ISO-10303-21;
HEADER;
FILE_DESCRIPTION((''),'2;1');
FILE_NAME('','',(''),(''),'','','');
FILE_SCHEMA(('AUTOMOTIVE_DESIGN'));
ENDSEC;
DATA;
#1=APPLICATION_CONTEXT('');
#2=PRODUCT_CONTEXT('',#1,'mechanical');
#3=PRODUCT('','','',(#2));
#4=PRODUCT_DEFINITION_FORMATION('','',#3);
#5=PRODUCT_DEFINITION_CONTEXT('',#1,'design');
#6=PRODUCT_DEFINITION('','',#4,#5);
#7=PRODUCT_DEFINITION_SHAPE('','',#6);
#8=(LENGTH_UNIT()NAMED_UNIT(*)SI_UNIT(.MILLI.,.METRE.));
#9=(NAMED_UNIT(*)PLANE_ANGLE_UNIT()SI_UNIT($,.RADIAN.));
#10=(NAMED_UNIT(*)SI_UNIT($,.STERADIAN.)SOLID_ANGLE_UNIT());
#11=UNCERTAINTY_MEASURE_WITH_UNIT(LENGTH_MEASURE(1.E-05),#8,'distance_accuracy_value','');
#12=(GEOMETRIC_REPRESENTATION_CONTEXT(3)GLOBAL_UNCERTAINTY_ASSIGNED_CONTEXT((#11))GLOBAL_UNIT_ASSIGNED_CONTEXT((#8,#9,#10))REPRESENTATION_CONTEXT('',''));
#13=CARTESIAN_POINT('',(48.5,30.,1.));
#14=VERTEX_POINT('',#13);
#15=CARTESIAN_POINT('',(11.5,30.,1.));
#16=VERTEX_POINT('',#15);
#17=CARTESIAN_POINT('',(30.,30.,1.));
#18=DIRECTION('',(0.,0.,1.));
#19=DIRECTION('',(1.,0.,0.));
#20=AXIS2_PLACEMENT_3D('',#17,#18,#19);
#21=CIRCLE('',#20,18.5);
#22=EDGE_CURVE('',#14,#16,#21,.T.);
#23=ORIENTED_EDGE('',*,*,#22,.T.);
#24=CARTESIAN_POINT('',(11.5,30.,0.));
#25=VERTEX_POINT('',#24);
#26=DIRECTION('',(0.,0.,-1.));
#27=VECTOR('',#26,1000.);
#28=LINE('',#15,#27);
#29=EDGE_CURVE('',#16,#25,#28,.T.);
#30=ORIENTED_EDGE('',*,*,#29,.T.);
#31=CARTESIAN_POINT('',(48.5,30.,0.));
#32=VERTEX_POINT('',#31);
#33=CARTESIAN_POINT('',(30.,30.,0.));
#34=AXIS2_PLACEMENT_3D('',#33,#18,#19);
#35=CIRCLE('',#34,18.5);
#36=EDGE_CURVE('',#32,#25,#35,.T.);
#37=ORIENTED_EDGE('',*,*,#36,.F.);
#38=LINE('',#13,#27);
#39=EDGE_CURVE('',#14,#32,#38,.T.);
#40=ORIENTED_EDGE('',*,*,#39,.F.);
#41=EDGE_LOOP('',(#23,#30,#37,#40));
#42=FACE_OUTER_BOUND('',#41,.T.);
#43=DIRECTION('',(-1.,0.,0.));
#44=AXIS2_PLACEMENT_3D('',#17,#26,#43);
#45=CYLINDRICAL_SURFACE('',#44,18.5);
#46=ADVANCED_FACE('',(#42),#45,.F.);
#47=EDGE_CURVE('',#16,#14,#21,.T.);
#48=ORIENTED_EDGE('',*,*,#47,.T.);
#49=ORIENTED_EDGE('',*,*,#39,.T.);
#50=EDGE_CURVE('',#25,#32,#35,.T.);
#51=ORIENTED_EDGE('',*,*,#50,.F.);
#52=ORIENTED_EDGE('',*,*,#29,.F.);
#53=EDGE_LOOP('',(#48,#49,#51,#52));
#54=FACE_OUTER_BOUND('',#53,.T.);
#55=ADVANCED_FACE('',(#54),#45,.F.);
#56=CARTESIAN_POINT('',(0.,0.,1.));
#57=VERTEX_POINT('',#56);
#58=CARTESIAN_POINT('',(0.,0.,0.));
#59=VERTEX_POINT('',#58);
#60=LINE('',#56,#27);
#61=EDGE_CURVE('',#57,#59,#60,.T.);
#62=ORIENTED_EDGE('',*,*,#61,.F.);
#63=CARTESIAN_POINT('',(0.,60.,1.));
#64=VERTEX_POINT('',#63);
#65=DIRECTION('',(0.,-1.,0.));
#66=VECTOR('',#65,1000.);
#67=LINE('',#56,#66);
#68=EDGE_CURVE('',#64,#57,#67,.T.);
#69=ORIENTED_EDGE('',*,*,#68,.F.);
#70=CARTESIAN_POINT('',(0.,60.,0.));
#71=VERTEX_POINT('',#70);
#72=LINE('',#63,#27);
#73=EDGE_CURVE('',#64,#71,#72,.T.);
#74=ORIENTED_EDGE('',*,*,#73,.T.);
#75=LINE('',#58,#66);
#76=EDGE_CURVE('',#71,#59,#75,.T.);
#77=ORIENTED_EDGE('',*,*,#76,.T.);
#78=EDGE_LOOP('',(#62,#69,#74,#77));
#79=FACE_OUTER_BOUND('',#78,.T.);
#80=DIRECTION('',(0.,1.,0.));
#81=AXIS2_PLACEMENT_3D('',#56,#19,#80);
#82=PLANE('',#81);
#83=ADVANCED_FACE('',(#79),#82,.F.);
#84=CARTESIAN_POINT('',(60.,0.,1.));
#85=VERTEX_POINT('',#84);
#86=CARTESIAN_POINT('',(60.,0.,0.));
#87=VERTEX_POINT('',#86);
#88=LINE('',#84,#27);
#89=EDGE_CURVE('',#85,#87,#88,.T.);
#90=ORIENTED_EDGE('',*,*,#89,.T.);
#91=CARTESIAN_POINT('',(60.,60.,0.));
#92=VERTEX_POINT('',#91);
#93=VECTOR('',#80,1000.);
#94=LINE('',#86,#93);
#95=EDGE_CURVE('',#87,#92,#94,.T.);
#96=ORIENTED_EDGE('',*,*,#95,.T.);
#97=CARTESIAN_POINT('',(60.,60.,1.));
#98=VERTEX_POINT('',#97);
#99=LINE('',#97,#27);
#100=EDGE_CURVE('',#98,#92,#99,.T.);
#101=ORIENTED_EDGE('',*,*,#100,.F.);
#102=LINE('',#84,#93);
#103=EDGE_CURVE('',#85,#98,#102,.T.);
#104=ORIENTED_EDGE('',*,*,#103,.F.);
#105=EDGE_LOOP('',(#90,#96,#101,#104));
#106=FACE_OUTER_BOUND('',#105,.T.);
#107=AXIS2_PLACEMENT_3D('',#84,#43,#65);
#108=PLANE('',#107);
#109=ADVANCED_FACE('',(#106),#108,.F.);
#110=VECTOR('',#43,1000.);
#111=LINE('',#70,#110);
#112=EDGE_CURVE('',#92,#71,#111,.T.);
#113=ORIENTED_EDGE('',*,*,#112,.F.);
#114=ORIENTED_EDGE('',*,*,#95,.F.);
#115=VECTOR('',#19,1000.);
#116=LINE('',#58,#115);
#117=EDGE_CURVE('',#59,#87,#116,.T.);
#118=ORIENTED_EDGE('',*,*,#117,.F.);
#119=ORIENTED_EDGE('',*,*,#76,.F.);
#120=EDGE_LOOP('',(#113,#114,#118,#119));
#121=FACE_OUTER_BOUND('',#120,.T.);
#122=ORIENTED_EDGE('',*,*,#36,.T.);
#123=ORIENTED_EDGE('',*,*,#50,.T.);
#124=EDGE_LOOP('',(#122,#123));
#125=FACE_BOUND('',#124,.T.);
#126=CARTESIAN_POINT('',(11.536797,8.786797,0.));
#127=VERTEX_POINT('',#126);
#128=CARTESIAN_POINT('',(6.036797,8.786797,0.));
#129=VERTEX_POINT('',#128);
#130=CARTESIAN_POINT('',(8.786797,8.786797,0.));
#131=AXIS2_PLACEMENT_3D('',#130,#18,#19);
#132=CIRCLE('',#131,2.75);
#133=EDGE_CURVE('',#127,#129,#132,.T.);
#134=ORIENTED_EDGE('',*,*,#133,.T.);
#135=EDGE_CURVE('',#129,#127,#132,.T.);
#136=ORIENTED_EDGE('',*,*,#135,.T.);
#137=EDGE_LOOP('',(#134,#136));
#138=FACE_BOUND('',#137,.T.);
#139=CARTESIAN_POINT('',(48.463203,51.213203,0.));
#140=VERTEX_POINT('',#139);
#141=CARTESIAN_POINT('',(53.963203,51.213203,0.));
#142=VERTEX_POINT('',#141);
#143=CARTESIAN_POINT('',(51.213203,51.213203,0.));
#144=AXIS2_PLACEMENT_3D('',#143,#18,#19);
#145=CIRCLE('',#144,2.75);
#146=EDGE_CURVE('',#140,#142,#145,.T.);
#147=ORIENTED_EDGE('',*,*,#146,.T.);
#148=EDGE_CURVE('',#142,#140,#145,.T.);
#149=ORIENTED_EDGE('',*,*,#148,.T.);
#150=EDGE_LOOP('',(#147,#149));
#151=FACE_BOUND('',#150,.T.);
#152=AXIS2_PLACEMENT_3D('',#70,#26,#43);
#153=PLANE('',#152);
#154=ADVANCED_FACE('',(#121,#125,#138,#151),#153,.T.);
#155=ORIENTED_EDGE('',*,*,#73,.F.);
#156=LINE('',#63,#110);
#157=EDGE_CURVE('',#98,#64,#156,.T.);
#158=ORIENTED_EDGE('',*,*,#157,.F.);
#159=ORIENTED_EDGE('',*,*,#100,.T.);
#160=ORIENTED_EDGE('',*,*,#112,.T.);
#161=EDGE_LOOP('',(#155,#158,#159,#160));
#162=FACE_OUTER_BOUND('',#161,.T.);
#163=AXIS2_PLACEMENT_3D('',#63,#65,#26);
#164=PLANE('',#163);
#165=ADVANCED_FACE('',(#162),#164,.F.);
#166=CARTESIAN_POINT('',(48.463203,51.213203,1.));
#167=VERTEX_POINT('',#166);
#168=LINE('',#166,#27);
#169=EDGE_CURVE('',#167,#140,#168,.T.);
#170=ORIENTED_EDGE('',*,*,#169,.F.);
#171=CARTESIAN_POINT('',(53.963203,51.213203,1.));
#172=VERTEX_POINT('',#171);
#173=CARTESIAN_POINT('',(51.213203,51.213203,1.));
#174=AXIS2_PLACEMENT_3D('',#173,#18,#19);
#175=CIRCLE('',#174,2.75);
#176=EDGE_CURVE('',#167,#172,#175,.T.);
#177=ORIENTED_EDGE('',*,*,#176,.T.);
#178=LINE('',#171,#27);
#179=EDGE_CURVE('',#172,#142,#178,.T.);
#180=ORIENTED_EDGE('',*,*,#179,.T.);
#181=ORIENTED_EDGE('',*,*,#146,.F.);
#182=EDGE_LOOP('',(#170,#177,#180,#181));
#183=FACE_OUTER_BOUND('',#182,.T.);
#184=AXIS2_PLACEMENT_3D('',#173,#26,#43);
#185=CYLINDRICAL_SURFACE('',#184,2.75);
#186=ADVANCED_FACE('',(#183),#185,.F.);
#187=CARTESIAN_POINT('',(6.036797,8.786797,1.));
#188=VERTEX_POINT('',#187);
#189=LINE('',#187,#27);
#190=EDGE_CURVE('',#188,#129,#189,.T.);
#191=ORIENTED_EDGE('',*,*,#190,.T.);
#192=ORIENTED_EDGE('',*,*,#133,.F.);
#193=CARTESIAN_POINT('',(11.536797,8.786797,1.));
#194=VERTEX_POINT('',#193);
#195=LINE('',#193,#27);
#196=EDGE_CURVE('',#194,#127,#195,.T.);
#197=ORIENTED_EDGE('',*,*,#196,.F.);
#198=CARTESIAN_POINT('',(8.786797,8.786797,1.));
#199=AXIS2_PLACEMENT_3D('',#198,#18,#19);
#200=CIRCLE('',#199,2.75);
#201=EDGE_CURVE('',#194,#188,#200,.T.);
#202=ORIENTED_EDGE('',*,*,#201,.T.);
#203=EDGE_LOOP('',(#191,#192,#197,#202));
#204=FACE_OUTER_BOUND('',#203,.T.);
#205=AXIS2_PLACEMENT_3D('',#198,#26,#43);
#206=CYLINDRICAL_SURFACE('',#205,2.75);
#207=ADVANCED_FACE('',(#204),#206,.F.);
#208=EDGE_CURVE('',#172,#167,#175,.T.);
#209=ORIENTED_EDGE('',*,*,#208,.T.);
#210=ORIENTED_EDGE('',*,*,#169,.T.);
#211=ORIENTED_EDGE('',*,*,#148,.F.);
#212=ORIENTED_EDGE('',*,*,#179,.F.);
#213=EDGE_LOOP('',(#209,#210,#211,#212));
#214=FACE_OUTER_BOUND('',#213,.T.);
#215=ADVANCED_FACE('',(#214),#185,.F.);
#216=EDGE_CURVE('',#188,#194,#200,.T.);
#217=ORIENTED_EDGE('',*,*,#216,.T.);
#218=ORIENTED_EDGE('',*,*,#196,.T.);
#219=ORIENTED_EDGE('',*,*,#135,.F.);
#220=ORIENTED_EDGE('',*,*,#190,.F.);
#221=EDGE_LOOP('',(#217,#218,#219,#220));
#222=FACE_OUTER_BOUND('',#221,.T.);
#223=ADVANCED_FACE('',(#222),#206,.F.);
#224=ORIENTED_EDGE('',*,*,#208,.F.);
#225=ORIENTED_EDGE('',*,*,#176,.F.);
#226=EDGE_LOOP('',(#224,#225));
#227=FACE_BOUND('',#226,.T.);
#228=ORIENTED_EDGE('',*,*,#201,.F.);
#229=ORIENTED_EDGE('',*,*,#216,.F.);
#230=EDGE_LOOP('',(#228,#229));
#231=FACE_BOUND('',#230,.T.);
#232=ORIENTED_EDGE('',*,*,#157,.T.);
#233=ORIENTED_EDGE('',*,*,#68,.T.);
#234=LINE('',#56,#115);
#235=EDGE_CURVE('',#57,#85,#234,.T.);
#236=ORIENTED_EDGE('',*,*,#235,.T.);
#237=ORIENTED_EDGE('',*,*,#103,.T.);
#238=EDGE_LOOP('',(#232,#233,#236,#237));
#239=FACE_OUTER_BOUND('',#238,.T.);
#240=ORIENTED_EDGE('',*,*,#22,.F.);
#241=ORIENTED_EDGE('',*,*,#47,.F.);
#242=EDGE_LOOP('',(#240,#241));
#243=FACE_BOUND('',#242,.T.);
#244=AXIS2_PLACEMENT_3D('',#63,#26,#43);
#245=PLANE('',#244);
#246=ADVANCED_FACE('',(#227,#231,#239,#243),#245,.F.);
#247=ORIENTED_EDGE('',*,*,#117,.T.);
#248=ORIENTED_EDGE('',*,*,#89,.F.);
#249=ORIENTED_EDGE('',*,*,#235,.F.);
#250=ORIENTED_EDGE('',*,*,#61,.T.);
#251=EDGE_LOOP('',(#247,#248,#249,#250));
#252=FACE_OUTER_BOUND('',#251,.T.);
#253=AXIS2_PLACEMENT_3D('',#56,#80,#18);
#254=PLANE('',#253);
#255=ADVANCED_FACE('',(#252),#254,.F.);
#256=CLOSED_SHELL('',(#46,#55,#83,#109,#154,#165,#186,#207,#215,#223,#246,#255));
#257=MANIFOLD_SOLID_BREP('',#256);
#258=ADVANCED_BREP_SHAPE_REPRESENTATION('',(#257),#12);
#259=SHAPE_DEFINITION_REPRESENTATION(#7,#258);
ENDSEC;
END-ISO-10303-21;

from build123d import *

# Parameters (mm, degrees)
SKETCH_1_W      = 60
SKETCH_1_H      = 60
SKETCH_1_R      = 18.5
SKETCH_1_R_2    = 2.75
EXTRUDE_1_DEPTH = 1


with BuildPart() as part:
    # 草图1 → 凸台-拉伸1 (new body)
    with BuildSketch(Plane.XY):
        with Locations((30, 30)):
            Rectangle(SKETCH_1_W, SKETCH_1_H)
        with Locations((30, 30)):
            Circle(SKETCH_1_R, mode=Mode.SUBTRACT)
        with Locations((8.786796564, 8.786796564)):
            Circle(SKETCH_1_R_2, mode=Mode.SUBTRACT)
        with Locations((51.213203436, 51.213203436)):
            Circle(SKETCH_1_R_2, mode=Mode.SUBTRACT)
    extrude(amount=EXTRUDE_1_DEPTH)


solid = part.part
